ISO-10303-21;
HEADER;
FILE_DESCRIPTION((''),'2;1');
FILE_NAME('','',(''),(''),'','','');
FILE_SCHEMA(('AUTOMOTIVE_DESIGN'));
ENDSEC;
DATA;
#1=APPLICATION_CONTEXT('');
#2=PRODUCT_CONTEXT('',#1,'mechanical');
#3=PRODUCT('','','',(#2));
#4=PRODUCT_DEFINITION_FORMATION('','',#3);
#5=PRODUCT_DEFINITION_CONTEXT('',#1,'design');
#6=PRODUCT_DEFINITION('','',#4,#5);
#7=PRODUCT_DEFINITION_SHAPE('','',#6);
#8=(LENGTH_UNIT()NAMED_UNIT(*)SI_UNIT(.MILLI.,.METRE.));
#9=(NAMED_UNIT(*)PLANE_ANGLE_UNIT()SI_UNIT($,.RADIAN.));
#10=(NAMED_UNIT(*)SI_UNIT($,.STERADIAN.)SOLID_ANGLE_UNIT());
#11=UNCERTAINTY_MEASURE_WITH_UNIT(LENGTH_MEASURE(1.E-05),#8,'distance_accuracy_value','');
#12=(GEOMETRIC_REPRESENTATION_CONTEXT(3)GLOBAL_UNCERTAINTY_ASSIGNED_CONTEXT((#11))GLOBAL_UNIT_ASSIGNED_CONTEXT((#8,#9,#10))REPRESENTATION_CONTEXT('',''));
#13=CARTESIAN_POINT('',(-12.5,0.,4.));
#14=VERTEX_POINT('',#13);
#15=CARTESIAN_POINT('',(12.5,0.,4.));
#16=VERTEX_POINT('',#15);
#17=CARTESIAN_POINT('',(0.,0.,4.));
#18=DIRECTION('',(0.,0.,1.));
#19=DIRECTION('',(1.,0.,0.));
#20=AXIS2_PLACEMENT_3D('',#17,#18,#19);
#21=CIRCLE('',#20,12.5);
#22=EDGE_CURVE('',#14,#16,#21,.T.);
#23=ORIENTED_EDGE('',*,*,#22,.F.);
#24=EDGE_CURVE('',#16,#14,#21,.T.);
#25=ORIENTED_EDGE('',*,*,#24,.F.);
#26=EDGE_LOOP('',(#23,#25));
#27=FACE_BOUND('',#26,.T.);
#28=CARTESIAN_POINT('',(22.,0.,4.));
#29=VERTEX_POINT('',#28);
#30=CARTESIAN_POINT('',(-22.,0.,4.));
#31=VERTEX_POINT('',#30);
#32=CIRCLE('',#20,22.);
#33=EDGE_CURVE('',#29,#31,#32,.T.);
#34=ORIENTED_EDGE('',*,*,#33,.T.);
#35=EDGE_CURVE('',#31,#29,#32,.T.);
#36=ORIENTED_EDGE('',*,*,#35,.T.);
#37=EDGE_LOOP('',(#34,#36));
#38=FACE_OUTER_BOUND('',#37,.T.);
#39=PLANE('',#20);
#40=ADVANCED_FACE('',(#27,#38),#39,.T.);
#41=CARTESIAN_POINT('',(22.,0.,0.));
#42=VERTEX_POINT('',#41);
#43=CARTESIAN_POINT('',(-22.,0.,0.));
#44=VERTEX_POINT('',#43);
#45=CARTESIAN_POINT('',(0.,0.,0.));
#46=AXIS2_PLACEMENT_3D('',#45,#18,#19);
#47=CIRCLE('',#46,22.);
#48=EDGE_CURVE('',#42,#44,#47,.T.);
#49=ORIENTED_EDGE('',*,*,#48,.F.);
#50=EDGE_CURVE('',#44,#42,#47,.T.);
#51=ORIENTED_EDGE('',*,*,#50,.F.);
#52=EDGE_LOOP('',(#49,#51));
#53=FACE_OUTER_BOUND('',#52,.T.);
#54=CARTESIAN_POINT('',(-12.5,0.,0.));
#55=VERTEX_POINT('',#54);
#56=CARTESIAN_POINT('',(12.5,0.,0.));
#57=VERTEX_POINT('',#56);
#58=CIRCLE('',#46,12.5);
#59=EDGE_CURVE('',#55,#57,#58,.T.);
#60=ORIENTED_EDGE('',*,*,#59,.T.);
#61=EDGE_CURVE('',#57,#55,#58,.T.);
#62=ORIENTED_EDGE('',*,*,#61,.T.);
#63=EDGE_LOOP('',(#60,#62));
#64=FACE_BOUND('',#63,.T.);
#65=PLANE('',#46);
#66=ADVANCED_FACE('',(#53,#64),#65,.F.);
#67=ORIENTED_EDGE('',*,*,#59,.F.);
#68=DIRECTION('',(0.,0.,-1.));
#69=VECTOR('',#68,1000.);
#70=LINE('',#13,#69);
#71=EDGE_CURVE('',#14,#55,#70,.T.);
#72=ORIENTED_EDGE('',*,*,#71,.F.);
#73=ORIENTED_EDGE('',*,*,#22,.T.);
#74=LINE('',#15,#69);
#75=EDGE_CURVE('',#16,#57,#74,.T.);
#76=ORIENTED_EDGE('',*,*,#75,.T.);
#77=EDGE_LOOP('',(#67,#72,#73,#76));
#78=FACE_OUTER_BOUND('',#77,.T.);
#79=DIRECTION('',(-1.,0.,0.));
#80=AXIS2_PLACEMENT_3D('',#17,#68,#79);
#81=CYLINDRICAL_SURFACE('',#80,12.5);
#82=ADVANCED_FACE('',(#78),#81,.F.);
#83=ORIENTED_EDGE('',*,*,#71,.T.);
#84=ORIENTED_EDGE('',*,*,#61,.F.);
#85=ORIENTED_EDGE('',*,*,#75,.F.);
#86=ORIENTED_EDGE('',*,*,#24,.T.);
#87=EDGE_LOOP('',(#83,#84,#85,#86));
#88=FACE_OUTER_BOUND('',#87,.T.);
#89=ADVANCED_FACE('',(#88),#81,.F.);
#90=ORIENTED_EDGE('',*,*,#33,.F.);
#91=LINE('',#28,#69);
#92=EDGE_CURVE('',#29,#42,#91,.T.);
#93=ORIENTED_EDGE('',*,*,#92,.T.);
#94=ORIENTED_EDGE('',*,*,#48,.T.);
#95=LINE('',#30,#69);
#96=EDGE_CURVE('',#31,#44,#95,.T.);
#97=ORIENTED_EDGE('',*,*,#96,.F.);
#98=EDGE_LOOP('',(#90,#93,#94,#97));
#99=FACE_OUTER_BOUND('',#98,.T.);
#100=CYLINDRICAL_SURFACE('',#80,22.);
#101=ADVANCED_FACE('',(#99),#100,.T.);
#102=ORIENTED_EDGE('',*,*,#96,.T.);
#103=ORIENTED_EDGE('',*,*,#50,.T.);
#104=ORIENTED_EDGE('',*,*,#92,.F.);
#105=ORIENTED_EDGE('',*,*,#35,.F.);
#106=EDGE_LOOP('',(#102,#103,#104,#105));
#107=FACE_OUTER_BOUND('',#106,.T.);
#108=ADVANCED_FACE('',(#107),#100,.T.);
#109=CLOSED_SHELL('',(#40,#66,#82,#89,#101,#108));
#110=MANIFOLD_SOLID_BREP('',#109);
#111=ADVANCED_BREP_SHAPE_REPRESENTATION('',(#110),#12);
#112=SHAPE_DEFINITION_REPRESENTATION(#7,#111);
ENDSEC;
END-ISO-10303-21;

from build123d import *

# Parameters (mm, degrees)
SKETCH_246_R    = 22
SKETCH_246_R_2  = 12.5
EXTRUDE_1_DEPTH = 4


with BuildPart() as part:
    # Sketch 246 → 拉伸1 (new body)
    with BuildSketch(Plane.XY):
        Circle(SKETCH_246_R)
        Circle(SKETCH_246_R_2, mode=Mode.SUBTRACT)
    extrude(amount=EXTRUDE_1_DEPTH)


solid = part.part
